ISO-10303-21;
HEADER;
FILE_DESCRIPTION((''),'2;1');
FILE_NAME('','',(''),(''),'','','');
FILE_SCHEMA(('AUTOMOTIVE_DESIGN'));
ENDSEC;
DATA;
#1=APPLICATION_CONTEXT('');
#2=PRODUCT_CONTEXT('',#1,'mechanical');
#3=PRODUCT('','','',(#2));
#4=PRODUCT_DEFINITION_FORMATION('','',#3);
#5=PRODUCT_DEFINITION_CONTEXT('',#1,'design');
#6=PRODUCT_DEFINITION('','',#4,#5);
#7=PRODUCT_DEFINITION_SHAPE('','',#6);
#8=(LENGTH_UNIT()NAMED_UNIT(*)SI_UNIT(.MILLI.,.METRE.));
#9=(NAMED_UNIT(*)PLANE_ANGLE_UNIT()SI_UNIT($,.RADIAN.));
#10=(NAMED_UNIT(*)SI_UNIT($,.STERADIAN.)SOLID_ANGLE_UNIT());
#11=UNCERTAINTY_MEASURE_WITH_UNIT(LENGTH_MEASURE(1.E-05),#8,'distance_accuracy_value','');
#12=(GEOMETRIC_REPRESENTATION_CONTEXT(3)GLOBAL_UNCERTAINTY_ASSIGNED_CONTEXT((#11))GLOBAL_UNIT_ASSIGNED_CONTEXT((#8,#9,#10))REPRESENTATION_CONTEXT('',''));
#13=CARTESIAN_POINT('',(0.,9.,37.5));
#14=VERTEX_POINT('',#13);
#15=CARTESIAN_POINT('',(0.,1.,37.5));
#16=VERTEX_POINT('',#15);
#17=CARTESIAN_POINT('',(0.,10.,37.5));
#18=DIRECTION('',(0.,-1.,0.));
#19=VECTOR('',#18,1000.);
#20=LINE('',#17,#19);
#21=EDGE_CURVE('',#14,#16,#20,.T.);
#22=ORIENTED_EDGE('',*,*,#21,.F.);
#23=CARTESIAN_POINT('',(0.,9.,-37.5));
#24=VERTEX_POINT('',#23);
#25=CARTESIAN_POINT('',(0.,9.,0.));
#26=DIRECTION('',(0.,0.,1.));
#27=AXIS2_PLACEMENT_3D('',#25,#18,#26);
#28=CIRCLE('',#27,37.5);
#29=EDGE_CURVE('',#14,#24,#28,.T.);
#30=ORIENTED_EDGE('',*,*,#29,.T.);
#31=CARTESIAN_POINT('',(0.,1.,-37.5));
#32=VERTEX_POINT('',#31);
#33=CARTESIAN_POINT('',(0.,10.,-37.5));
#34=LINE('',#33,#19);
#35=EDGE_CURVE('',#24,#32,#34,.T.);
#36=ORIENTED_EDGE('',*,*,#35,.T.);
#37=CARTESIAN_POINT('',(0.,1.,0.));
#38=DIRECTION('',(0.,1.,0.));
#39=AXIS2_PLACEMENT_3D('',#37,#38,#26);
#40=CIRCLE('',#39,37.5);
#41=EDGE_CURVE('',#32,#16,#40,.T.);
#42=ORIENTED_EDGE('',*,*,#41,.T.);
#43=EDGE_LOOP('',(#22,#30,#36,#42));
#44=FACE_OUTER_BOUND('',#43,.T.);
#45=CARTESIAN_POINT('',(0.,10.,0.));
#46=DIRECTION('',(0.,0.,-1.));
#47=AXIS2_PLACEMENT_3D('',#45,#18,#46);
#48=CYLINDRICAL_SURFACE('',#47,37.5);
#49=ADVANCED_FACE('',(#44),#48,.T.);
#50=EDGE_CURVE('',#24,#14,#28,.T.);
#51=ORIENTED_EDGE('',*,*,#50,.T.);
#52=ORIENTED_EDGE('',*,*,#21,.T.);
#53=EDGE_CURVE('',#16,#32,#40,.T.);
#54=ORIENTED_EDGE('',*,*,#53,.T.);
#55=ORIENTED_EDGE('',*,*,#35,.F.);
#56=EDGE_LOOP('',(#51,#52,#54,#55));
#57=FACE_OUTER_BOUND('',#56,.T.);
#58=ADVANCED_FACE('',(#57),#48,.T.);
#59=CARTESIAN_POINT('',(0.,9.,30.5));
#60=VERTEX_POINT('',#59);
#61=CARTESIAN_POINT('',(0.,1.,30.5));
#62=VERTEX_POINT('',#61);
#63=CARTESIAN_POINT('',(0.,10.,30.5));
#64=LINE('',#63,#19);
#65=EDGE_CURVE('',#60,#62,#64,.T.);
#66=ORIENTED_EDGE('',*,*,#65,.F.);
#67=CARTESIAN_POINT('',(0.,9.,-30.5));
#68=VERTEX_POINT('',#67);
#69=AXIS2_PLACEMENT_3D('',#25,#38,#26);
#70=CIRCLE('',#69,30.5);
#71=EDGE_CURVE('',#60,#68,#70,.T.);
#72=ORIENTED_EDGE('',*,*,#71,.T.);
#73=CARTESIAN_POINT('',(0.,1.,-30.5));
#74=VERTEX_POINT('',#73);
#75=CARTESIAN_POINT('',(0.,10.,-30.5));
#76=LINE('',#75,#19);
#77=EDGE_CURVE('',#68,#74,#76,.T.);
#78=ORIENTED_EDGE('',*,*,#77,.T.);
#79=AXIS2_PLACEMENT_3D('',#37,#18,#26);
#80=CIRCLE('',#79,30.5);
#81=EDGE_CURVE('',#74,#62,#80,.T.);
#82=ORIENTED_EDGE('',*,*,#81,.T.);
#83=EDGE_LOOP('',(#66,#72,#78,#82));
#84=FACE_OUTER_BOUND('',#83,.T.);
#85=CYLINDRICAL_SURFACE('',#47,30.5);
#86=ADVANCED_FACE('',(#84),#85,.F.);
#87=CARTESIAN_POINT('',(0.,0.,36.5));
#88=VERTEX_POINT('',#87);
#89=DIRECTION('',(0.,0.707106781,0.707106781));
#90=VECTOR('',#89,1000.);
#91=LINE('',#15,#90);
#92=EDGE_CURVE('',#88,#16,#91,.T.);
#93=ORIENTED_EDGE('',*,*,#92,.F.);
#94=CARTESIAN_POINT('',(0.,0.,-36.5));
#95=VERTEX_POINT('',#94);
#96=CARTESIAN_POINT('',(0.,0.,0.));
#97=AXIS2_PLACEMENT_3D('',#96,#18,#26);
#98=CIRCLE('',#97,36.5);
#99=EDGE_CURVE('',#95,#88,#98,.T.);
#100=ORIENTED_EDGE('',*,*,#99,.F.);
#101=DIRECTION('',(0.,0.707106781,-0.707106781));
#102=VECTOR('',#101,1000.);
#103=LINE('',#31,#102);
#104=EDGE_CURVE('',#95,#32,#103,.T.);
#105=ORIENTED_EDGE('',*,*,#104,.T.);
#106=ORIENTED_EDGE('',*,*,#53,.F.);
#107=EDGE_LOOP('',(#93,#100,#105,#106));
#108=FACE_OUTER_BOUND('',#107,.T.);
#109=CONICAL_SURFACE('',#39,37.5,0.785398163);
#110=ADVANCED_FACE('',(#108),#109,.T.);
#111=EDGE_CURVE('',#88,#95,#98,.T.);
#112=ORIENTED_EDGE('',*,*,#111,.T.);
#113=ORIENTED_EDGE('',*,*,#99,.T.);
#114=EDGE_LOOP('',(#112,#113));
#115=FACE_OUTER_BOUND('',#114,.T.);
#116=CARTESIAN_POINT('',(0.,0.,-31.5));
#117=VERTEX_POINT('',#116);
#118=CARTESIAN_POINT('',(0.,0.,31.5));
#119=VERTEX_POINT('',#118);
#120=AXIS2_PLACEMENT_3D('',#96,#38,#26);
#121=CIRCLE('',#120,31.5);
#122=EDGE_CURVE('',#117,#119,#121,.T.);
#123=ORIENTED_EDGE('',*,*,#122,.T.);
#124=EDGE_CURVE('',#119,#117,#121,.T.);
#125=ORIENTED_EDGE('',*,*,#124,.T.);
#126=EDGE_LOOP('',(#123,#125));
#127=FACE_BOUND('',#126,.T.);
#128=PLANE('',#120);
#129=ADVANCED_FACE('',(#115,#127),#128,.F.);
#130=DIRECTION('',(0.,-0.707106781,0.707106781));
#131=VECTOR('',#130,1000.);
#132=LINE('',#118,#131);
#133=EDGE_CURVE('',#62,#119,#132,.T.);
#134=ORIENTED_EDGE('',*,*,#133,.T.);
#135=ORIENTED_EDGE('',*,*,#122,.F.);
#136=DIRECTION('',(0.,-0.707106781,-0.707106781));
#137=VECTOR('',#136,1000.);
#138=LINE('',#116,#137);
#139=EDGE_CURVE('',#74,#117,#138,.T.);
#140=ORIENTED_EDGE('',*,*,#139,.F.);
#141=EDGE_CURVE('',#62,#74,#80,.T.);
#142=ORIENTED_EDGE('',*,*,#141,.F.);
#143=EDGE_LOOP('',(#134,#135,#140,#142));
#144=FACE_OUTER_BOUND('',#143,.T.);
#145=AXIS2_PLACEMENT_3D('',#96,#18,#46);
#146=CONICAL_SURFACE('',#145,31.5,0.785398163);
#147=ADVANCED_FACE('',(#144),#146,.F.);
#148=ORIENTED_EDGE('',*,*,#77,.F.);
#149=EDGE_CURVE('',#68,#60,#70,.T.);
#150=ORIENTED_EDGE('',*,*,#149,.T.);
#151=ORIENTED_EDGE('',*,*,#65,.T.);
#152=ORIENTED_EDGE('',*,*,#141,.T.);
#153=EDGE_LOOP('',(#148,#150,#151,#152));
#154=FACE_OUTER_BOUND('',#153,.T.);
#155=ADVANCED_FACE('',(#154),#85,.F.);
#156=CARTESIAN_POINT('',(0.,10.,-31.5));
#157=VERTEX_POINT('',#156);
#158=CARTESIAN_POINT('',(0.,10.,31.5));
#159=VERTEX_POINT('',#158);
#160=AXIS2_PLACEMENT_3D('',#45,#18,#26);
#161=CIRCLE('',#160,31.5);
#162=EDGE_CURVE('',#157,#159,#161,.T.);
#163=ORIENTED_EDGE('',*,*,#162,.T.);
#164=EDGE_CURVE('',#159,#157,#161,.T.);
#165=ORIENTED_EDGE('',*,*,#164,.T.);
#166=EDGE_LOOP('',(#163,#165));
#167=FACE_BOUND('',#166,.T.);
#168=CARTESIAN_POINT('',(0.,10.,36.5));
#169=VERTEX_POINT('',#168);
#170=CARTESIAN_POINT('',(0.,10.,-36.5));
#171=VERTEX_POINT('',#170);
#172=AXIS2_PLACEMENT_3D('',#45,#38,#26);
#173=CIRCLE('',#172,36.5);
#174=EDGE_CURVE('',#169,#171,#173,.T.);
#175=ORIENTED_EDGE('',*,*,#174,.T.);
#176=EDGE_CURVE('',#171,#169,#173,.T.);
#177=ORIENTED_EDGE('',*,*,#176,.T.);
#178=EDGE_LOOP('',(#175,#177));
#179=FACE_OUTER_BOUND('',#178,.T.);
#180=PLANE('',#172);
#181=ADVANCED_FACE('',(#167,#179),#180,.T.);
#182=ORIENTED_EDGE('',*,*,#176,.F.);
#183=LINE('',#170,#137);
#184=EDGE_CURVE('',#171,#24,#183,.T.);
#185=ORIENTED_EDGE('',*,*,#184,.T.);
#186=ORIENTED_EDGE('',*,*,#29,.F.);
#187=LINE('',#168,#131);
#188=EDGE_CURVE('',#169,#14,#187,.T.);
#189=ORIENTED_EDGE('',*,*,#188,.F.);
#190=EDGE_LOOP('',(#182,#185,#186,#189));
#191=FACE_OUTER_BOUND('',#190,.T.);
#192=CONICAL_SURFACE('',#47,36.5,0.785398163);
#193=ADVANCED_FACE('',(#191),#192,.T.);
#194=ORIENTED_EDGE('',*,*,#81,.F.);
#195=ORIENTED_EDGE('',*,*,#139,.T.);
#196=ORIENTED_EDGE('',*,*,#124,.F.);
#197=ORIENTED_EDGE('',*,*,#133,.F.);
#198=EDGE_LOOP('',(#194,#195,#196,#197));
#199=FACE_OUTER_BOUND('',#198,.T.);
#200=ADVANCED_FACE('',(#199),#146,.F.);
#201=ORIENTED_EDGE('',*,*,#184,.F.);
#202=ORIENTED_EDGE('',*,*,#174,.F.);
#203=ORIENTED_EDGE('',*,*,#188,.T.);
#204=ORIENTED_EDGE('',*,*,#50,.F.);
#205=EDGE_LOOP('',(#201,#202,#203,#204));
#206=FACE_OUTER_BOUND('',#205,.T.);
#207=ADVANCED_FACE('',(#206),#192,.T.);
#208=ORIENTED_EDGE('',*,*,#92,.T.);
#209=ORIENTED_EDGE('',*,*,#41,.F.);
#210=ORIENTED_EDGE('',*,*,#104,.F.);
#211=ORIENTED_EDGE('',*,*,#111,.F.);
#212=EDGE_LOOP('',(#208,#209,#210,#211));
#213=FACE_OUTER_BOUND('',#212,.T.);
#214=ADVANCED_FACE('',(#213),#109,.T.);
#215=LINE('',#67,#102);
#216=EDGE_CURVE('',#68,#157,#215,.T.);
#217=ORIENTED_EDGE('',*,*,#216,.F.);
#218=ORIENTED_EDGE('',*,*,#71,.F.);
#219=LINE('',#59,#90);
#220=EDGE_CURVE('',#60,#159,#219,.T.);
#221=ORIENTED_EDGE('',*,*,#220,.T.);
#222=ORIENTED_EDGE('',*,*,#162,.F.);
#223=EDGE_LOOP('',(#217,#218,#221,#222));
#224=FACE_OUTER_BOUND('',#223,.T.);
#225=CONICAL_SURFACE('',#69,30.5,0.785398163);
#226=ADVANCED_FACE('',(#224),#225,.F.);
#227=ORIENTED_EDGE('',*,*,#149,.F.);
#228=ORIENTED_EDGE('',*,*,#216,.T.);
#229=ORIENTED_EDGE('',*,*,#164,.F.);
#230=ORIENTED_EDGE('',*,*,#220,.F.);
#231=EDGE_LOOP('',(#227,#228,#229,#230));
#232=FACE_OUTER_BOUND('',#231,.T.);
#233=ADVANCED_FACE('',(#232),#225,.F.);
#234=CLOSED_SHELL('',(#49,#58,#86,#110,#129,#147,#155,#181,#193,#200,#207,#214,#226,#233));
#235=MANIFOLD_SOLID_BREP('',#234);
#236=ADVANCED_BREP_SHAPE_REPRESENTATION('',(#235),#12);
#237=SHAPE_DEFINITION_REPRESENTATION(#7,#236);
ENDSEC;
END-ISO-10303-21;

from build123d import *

# Parameters (mm, degrees)
SKETCH1_R           = 37.5
SKETCH1_R_2         = 30.5
BOSS_EXTRUDE1_DEPTH = 10
CHAMFER1_SIZE       = 1


with BuildPart() as part:
    # Sketch1 → Boss-Extrude1 (new body)
    with BuildSketch(Plane(origin=(0, 0, 0), x_dir=(1, 0, 0), z_dir=(0, 1, 0))):
        with Locations(Location((0, 0, 0), (0, 0, 270))):
            Circle(SKETCH1_R)
        with Locations(Location((0, 0, 0), (0, 0, 270))):
            Circle(SKETCH1_R_2, mode=Mode.SUBTRACT)
    extrude(amount=BOSS_EXTRUDE1_DEPTH)

    # Chamfer1
    chamfer1_edges = [part.edges().sort_by_distance(p)[0] for p in [
        (0, 0, -37.5),
        (0, 10, -37.5),
        (0, 0, -30.5),
        (0, 10, -30.5),
    ]]
    chamfer(chamfer1_edges, length=CHAMFER1_SIZE)


solid = part.part
